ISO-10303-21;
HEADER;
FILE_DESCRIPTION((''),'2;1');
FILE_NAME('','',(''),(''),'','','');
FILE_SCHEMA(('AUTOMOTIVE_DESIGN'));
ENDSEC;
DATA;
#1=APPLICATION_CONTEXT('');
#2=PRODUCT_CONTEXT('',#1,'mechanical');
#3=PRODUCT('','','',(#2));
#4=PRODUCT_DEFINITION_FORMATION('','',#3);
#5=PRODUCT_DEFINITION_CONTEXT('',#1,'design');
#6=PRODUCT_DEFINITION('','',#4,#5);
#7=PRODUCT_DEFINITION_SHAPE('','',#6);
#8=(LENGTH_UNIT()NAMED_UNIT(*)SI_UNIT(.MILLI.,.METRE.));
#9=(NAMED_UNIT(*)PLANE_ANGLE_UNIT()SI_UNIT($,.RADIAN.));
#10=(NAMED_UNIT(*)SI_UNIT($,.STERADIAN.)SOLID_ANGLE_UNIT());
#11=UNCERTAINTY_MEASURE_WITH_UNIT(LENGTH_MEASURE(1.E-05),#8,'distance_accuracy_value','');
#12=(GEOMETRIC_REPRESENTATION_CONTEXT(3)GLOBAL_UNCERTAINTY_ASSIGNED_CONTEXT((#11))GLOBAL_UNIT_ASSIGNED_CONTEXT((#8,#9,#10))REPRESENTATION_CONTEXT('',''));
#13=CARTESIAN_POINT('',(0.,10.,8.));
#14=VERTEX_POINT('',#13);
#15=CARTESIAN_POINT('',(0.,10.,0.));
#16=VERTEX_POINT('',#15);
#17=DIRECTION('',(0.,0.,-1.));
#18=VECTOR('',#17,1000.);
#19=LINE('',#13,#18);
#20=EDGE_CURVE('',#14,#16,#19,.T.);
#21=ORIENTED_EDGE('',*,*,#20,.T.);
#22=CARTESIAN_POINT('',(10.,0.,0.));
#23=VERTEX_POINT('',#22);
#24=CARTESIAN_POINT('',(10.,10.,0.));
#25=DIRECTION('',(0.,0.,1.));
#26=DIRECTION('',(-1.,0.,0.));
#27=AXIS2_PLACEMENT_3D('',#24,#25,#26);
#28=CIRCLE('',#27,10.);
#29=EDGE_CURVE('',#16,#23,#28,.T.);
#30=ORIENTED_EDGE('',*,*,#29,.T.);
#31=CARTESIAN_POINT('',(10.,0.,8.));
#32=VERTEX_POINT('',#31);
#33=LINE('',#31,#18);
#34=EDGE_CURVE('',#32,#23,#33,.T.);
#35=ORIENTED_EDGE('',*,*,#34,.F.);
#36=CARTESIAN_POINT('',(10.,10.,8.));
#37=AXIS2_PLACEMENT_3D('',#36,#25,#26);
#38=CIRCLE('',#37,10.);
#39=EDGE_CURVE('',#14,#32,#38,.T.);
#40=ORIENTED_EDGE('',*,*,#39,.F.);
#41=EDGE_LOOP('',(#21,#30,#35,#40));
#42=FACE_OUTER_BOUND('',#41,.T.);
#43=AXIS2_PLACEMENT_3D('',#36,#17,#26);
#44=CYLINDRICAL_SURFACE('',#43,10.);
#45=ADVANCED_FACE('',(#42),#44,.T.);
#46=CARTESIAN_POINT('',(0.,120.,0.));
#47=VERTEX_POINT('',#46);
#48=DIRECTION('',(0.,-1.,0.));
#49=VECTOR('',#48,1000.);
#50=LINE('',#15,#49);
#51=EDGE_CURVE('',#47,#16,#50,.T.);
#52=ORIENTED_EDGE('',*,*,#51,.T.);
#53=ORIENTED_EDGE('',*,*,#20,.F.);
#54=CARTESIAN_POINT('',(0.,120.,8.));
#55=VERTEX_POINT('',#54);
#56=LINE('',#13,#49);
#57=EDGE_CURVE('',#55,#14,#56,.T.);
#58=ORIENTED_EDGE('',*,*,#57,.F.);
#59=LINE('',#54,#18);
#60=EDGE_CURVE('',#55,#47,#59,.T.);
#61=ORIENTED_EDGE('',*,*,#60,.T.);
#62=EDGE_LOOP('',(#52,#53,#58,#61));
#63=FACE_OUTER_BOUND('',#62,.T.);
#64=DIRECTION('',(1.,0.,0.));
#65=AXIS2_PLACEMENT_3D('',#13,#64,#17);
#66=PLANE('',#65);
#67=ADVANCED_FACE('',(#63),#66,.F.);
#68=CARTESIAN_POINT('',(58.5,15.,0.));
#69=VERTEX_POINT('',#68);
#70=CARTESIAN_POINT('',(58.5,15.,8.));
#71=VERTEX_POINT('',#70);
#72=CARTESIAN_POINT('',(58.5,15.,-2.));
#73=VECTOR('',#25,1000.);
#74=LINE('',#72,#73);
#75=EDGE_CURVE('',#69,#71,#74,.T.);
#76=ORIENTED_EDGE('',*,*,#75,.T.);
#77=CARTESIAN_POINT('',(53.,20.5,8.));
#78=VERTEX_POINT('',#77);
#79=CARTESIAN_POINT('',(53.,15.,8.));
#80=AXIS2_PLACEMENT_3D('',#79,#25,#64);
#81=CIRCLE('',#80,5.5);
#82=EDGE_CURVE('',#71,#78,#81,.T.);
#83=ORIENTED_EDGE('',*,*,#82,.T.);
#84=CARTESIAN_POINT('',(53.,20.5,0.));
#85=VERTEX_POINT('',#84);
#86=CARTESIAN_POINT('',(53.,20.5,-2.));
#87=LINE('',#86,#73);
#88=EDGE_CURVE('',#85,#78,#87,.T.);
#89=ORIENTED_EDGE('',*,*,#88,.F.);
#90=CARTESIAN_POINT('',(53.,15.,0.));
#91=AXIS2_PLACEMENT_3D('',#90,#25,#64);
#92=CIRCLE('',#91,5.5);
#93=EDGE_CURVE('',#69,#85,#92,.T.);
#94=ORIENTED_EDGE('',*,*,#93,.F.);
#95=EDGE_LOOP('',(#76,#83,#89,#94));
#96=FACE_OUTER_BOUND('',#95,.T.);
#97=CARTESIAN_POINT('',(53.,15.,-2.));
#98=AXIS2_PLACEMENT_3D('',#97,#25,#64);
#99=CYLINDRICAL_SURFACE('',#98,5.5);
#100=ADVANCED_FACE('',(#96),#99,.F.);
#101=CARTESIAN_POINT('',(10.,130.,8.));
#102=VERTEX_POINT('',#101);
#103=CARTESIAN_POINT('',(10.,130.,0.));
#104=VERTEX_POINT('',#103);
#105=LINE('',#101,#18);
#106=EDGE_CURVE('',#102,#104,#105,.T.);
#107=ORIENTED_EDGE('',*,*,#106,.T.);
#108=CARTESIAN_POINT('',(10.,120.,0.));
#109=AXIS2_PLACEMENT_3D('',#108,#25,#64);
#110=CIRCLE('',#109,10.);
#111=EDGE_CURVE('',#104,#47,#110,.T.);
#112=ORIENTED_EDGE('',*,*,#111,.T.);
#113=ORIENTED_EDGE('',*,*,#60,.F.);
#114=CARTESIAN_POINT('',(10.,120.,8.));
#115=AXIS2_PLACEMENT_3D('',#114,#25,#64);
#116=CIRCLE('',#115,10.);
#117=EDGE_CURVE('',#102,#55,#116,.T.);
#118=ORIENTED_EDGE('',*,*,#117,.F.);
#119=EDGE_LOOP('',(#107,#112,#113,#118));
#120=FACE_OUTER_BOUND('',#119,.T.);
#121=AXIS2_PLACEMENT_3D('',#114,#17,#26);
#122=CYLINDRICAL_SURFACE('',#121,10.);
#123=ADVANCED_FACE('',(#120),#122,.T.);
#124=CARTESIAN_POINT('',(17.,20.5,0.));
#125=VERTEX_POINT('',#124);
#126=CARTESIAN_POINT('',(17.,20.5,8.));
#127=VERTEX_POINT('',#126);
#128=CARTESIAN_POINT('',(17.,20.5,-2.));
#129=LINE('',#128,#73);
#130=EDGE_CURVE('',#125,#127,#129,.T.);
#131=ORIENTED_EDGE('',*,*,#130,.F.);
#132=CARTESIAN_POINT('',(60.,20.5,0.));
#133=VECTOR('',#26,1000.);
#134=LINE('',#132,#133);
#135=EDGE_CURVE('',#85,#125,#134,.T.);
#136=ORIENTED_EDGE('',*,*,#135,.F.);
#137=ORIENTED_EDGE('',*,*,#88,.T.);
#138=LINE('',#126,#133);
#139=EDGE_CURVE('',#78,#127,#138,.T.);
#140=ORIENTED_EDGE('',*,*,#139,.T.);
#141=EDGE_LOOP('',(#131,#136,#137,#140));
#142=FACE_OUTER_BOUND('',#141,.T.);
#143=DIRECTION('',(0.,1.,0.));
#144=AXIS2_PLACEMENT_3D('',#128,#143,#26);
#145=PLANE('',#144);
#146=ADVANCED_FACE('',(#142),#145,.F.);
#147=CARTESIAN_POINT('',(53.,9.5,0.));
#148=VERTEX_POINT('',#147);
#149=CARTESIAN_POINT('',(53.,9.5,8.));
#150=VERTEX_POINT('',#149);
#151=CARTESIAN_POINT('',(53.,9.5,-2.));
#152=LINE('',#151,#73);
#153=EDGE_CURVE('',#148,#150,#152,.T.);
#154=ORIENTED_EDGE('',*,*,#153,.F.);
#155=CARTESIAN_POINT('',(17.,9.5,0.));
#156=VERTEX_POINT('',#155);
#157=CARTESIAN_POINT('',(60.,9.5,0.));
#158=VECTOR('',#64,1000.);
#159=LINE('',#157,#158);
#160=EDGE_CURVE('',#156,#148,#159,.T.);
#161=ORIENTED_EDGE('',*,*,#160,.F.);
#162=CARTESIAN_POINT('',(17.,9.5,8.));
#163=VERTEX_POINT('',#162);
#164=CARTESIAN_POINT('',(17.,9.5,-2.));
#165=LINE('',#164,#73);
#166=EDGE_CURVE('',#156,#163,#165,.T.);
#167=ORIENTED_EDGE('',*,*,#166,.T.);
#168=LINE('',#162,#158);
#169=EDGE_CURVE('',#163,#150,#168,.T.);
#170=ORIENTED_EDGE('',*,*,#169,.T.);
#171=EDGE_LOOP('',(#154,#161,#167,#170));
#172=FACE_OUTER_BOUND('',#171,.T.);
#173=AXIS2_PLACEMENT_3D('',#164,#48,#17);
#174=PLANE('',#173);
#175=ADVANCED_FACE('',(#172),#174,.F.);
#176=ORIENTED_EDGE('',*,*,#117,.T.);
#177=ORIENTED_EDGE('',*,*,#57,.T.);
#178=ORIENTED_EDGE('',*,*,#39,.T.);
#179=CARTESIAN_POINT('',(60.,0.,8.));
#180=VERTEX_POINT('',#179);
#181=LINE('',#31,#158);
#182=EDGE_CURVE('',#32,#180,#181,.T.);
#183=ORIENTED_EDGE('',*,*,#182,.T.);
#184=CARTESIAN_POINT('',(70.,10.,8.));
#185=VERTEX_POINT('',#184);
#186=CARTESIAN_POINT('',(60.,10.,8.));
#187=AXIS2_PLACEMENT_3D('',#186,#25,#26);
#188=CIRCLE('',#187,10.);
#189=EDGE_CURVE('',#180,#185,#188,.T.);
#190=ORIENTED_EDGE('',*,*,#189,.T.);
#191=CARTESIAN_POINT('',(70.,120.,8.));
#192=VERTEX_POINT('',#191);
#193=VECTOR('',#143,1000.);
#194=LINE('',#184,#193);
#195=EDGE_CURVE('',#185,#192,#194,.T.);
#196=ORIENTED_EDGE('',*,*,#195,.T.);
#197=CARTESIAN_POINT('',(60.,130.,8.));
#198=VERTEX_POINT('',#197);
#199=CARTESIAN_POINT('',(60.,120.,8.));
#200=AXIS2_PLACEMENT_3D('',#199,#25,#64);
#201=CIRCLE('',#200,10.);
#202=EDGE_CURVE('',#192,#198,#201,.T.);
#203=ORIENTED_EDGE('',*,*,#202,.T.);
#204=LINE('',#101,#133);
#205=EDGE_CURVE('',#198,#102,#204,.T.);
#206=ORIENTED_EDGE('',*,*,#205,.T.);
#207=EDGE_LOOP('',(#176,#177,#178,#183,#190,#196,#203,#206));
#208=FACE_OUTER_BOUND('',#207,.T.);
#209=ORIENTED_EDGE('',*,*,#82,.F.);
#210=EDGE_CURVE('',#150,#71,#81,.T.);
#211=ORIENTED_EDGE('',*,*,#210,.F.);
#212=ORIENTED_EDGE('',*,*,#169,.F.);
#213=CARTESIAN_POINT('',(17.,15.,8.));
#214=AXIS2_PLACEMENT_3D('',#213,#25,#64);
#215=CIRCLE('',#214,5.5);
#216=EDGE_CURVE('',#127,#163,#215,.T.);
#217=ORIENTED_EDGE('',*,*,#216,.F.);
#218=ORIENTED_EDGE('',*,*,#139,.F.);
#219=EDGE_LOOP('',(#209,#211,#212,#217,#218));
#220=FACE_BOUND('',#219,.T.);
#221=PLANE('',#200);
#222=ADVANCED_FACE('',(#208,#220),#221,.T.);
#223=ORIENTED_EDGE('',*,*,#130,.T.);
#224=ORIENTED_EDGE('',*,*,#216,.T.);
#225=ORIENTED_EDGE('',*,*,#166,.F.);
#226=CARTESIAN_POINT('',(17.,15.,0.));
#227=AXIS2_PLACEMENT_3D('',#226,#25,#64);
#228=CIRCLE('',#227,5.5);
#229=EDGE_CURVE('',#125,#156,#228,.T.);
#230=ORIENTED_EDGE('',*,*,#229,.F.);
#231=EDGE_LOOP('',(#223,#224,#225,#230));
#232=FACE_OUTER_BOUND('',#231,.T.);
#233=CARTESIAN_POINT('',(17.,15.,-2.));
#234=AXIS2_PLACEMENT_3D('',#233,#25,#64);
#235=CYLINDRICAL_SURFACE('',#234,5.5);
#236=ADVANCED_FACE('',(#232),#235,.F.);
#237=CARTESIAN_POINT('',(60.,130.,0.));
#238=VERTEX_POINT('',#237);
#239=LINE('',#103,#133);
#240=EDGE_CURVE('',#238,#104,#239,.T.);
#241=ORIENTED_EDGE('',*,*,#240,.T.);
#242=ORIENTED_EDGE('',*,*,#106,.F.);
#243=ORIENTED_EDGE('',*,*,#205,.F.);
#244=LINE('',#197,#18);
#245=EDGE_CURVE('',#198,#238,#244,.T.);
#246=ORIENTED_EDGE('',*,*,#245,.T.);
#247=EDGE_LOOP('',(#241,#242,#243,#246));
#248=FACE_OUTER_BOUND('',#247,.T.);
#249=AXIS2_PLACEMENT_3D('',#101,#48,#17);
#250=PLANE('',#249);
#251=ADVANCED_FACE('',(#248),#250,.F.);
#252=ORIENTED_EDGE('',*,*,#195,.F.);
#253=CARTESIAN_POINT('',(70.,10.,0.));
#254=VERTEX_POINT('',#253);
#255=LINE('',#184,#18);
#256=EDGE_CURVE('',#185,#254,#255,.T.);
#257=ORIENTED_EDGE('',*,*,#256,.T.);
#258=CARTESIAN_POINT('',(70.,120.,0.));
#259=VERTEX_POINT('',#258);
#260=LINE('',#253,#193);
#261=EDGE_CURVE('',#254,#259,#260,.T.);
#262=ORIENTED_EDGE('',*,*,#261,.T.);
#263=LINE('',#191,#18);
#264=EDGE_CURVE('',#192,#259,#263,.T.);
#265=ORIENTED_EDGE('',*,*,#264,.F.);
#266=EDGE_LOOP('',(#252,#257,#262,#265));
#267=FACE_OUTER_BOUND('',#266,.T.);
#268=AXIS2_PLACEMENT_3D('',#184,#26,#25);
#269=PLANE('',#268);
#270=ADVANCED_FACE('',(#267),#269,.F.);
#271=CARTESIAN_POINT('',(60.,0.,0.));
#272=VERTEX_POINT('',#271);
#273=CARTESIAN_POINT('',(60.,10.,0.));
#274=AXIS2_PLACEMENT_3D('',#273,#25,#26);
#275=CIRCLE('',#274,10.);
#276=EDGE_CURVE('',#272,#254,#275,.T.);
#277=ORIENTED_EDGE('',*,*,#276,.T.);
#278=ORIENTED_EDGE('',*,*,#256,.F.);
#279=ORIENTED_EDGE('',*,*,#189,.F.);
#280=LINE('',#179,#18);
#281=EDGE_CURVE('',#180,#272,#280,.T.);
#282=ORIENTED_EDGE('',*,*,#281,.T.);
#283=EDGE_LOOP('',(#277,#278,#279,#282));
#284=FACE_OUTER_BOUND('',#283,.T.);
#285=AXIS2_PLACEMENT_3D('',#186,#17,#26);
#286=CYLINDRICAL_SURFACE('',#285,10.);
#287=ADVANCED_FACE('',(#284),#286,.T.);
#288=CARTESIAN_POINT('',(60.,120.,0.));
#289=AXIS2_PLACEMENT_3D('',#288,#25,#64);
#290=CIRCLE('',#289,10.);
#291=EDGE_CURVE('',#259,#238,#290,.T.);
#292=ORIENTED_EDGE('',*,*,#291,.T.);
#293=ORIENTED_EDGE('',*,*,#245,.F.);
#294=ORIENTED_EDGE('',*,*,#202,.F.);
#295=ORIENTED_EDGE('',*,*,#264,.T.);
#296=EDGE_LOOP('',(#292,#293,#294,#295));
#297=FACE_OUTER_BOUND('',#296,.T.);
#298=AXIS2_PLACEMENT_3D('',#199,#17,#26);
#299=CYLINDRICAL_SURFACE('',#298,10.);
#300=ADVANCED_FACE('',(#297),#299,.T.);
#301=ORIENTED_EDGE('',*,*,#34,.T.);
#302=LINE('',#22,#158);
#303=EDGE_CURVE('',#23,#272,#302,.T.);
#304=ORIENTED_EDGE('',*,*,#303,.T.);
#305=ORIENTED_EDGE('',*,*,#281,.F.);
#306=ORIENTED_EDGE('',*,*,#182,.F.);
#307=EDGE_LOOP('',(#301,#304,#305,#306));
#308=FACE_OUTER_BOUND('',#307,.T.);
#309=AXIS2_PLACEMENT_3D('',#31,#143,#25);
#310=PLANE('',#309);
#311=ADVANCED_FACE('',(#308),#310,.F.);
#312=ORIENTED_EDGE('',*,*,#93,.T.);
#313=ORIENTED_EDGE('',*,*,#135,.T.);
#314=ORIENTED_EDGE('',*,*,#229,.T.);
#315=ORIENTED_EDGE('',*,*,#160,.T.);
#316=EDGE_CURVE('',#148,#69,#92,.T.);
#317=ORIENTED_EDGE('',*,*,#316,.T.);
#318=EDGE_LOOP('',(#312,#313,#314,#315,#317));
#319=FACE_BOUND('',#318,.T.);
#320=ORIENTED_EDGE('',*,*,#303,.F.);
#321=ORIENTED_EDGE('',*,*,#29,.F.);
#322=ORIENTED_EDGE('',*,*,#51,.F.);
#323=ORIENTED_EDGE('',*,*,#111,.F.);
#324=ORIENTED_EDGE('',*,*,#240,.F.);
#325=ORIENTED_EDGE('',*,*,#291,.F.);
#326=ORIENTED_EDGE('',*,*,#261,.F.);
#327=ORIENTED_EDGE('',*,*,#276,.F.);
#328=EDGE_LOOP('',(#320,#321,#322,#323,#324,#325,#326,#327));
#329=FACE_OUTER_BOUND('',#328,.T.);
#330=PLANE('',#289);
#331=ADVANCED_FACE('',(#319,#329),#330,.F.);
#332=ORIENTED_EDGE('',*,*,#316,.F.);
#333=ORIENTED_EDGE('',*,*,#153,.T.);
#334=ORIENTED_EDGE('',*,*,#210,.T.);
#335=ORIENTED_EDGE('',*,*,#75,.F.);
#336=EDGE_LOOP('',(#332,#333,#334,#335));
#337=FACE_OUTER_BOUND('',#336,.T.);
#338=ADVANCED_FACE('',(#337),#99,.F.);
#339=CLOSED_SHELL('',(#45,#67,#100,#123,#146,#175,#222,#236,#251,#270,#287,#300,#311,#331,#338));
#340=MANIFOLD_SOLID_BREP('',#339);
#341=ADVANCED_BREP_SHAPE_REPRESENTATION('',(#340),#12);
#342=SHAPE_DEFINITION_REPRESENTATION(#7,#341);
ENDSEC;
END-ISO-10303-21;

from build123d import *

# Parameters (mm, degrees)
BOSS_EXTRUDE1_DEPTH = 8
CUT_EXTRUDE1_DEPTH  = 10


with BuildPart() as part:
    # Sketch1 → Boss-Extrude1 (new body)
    with BuildSketch(Plane.XY):
        with BuildLine():
            Line((10, 0), (60, 0))
            ThreePointArc((60, 0), (67.071067812, 2.928932188), (70, 10))
            Line((70, 10), (70, 120))
            ThreePointArc((70, 120), (67.071067812, 127.071067812), (60, 130))
            Line((60, 130), (10, 130))
            ThreePointArc((10, 130), (2.928932188, 127.071067812), (0, 120))
            Line((0, 120), (0, 10))
            ThreePointArc((0, 10), (2.928932188, 2.928932188), (10, 0))
        make_face()
    extrude(amount=BOSS_EXTRUDE1_DEPTH)

    # Sketch2 → Cut-Extrude1 (cut)
    with BuildSketch(Plane.XY.offset(8)):
        with BuildLine():
            Line((17, 20.5), (53, 20.5))
            ThreePointArc((53, 20.5), (58.5, 15), (53, 9.5))
            Line((53, 9.5), (17, 9.5))
            ThreePointArc((17, 9.5), (11.5, 15), (17, 20.5))
        make_face()
    extrude(amount=-CUT_EXTRUDE1_DEPTH, mode=Mode.SUBTRACT)


solid = part.part
